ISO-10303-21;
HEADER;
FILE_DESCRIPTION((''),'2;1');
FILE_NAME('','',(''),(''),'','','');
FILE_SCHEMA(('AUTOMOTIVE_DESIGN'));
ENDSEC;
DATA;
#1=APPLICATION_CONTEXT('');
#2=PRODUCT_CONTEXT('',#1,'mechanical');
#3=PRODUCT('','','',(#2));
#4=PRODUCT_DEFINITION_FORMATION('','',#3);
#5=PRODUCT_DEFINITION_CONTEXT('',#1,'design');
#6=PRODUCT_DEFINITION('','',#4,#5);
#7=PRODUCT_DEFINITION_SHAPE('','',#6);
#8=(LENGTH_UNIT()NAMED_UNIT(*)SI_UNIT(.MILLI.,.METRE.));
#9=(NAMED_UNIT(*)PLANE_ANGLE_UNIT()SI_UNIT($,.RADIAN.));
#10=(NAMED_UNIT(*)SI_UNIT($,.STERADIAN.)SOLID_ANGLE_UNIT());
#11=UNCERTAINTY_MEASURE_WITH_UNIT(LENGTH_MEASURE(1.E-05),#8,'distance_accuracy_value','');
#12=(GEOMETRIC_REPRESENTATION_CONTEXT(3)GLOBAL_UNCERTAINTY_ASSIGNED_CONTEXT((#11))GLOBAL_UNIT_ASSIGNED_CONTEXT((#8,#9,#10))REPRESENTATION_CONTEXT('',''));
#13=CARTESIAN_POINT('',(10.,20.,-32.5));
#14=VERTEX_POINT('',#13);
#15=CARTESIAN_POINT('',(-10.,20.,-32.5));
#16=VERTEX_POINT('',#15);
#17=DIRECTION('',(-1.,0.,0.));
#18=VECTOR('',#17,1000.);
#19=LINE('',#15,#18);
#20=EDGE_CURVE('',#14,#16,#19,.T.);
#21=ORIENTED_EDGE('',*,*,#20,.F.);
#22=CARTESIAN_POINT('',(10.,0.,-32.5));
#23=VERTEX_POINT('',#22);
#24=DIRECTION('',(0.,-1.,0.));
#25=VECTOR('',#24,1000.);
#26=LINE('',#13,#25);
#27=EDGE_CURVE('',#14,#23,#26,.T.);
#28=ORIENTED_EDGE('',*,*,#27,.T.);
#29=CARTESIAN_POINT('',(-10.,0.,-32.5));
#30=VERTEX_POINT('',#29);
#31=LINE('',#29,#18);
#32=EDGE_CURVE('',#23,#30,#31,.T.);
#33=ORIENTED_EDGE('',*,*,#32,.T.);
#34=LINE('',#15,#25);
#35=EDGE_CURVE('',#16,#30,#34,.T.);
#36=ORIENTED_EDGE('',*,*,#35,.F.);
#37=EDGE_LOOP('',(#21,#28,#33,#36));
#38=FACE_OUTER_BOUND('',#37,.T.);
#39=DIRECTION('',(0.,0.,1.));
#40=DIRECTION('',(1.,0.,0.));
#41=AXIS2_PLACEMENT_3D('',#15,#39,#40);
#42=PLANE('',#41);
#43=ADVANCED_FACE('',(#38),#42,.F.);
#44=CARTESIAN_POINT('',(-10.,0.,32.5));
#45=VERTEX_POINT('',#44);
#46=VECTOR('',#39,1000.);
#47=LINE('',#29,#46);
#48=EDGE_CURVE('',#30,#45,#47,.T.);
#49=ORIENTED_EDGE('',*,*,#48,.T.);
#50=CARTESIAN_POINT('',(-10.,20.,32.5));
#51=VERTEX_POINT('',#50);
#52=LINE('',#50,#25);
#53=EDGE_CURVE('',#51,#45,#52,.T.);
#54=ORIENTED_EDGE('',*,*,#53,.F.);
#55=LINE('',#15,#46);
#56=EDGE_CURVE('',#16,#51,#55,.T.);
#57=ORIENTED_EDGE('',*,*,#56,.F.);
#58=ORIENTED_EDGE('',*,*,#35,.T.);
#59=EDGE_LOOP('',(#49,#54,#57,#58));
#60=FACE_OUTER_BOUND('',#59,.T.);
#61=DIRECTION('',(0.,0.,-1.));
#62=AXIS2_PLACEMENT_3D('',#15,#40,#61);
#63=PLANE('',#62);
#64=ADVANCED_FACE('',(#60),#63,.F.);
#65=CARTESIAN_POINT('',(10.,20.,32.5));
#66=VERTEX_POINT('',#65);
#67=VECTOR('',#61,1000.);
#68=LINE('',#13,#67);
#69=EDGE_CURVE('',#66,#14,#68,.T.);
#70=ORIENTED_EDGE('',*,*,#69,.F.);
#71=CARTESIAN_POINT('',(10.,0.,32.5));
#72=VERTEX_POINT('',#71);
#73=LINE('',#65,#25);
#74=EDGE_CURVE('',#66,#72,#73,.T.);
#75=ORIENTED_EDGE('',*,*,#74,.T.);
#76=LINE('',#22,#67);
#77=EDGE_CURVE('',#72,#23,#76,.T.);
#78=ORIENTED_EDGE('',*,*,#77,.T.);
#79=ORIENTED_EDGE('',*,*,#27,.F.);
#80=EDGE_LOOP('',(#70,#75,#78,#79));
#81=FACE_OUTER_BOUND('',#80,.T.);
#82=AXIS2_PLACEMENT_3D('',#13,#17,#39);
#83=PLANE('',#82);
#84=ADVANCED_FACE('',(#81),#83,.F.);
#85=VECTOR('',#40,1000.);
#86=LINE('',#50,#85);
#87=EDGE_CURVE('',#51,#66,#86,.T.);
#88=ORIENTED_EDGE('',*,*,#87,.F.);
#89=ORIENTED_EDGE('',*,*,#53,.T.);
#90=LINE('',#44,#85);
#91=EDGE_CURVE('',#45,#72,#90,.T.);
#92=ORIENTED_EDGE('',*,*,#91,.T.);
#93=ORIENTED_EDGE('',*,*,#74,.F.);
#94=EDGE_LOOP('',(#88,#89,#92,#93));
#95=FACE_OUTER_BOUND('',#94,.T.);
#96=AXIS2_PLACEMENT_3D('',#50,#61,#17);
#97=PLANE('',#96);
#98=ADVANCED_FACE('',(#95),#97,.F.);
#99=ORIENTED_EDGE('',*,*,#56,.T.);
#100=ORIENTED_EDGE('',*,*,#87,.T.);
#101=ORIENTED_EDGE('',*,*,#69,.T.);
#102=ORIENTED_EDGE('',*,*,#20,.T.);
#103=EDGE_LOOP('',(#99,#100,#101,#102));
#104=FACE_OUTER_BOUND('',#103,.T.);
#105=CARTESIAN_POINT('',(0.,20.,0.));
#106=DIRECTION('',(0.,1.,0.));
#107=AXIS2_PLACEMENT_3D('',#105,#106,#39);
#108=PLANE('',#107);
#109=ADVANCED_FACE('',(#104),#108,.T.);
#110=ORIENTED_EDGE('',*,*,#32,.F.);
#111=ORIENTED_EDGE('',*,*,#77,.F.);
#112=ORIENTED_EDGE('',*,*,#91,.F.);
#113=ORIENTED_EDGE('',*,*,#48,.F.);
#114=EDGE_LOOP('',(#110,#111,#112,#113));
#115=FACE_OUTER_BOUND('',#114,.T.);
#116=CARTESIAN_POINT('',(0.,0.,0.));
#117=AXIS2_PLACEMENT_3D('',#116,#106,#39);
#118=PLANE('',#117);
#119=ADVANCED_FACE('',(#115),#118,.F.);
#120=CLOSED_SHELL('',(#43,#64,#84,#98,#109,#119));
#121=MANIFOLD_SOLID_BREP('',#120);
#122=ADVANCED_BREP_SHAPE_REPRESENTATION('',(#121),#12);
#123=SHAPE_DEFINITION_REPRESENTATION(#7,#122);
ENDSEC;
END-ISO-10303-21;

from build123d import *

# Parameters (mm, degrees)
SKETCH1_W           = 20
SKETCH1_H           = 65
BOSS_EXTRUDE1_DEPTH = 20


with BuildPart() as part:
    # Sketch1 → Boss-Extrude1 (new body)
    with BuildSketch(Plane(origin=(0, 0, 0), x_dir=(1, 0, 0), z_dir=(0, 1, 0))):
        Rectangle(SKETCH1_W, SKETCH1_H)
    extrude(amount=BOSS_EXTRUDE1_DEPTH)


solid = part.part
